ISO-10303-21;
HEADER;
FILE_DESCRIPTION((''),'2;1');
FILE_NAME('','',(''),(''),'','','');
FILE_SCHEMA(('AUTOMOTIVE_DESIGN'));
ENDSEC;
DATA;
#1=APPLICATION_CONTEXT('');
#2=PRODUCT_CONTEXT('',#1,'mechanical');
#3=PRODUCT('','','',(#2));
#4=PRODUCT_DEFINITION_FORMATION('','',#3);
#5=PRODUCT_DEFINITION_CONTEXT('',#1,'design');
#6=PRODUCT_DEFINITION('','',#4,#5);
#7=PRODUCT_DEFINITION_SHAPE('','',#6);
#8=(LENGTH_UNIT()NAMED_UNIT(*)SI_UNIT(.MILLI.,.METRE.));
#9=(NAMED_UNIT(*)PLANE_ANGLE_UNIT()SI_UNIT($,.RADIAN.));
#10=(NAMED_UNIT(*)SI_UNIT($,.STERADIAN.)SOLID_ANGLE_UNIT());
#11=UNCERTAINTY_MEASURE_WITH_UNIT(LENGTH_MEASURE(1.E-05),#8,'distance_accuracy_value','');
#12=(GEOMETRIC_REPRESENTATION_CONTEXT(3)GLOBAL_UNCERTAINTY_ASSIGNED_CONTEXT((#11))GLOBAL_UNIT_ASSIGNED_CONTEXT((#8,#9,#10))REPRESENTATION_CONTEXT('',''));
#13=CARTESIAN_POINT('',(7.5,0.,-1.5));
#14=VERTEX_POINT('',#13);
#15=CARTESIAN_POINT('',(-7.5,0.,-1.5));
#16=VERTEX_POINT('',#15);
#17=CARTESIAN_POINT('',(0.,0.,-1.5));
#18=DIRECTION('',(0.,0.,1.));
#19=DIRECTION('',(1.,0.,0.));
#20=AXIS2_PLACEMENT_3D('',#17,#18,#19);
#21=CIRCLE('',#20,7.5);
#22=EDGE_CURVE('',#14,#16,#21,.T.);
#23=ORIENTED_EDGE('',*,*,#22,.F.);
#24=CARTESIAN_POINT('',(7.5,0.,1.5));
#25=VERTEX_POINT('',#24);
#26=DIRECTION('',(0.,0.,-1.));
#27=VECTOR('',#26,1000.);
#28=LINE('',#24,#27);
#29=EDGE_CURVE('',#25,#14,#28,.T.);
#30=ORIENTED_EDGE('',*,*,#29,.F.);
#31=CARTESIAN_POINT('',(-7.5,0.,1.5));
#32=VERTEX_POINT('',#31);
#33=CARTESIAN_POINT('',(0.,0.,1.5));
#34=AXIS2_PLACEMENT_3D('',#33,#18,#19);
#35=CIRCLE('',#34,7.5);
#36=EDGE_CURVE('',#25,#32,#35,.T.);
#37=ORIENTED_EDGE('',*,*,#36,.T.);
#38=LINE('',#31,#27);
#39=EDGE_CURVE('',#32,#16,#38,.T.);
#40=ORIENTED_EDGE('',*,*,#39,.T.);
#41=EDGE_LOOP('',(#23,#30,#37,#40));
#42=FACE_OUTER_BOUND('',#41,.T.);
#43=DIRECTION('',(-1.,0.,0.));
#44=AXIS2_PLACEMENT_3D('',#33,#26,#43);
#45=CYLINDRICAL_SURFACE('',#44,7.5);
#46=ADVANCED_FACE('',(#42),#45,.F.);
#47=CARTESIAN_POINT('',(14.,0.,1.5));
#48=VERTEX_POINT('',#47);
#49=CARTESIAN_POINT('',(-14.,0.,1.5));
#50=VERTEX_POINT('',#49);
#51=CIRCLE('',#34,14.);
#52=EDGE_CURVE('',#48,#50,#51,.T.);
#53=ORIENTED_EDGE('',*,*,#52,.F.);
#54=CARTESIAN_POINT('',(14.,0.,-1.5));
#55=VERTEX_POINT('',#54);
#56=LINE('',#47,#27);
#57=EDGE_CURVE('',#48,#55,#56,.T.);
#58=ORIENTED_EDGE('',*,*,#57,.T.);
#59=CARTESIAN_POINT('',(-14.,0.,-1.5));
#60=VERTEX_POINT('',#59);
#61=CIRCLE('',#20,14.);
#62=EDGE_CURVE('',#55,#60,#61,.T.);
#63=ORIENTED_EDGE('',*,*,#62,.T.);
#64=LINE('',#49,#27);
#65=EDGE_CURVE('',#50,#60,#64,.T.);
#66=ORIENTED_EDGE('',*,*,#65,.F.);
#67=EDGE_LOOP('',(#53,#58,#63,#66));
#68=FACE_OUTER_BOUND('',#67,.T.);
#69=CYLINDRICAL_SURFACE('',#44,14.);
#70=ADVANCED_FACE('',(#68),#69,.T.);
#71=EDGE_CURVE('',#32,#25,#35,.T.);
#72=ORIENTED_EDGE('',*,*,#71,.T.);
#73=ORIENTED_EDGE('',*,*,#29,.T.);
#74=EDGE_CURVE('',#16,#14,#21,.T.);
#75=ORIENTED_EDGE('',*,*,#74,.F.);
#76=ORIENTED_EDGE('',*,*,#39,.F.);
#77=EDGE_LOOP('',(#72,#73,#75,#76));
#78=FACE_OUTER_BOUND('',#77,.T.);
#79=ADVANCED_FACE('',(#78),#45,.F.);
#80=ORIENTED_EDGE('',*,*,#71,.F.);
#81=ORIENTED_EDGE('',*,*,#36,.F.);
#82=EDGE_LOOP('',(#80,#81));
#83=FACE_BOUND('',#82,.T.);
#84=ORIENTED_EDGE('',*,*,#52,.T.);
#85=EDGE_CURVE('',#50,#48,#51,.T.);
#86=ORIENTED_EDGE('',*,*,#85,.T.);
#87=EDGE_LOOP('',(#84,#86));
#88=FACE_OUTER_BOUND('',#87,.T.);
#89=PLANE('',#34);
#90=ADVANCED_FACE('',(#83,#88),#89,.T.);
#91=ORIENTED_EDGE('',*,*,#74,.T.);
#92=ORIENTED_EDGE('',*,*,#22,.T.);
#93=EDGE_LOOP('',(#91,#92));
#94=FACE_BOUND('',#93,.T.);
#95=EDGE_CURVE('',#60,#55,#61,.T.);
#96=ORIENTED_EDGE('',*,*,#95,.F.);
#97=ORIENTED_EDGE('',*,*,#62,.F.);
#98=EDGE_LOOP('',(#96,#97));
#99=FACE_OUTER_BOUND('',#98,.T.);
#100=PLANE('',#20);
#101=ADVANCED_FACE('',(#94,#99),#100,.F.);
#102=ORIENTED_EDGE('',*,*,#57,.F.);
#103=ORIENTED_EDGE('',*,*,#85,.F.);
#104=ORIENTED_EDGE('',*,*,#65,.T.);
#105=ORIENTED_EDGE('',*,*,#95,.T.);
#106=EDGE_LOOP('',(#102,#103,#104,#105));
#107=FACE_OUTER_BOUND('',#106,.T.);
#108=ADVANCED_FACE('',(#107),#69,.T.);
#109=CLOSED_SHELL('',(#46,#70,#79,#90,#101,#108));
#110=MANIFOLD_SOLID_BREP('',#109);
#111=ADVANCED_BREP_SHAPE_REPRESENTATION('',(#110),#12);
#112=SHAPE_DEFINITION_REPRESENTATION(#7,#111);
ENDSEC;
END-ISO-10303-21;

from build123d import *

# Parameters (mm, degrees)
WASHER_PROFILE_28_15_R   = 14
WASHER_PROFILE_28_15_R_2 = 7.5
WASHER_BODY_3MM_DEPTH    = 1.5


with BuildPart() as part:
    # Washer Profile Ø28-Ø15 → Washer Body 3mm (new, symmetric)
    with BuildSketch(Plane.XY):
        Circle(WASHER_PROFILE_28_15_R)
        Circle(WASHER_PROFILE_28_15_R_2, mode=Mode.SUBTRACT)
    extrude(amount=WASHER_BODY_3MM_DEPTH, both=True)


solid = part.part
